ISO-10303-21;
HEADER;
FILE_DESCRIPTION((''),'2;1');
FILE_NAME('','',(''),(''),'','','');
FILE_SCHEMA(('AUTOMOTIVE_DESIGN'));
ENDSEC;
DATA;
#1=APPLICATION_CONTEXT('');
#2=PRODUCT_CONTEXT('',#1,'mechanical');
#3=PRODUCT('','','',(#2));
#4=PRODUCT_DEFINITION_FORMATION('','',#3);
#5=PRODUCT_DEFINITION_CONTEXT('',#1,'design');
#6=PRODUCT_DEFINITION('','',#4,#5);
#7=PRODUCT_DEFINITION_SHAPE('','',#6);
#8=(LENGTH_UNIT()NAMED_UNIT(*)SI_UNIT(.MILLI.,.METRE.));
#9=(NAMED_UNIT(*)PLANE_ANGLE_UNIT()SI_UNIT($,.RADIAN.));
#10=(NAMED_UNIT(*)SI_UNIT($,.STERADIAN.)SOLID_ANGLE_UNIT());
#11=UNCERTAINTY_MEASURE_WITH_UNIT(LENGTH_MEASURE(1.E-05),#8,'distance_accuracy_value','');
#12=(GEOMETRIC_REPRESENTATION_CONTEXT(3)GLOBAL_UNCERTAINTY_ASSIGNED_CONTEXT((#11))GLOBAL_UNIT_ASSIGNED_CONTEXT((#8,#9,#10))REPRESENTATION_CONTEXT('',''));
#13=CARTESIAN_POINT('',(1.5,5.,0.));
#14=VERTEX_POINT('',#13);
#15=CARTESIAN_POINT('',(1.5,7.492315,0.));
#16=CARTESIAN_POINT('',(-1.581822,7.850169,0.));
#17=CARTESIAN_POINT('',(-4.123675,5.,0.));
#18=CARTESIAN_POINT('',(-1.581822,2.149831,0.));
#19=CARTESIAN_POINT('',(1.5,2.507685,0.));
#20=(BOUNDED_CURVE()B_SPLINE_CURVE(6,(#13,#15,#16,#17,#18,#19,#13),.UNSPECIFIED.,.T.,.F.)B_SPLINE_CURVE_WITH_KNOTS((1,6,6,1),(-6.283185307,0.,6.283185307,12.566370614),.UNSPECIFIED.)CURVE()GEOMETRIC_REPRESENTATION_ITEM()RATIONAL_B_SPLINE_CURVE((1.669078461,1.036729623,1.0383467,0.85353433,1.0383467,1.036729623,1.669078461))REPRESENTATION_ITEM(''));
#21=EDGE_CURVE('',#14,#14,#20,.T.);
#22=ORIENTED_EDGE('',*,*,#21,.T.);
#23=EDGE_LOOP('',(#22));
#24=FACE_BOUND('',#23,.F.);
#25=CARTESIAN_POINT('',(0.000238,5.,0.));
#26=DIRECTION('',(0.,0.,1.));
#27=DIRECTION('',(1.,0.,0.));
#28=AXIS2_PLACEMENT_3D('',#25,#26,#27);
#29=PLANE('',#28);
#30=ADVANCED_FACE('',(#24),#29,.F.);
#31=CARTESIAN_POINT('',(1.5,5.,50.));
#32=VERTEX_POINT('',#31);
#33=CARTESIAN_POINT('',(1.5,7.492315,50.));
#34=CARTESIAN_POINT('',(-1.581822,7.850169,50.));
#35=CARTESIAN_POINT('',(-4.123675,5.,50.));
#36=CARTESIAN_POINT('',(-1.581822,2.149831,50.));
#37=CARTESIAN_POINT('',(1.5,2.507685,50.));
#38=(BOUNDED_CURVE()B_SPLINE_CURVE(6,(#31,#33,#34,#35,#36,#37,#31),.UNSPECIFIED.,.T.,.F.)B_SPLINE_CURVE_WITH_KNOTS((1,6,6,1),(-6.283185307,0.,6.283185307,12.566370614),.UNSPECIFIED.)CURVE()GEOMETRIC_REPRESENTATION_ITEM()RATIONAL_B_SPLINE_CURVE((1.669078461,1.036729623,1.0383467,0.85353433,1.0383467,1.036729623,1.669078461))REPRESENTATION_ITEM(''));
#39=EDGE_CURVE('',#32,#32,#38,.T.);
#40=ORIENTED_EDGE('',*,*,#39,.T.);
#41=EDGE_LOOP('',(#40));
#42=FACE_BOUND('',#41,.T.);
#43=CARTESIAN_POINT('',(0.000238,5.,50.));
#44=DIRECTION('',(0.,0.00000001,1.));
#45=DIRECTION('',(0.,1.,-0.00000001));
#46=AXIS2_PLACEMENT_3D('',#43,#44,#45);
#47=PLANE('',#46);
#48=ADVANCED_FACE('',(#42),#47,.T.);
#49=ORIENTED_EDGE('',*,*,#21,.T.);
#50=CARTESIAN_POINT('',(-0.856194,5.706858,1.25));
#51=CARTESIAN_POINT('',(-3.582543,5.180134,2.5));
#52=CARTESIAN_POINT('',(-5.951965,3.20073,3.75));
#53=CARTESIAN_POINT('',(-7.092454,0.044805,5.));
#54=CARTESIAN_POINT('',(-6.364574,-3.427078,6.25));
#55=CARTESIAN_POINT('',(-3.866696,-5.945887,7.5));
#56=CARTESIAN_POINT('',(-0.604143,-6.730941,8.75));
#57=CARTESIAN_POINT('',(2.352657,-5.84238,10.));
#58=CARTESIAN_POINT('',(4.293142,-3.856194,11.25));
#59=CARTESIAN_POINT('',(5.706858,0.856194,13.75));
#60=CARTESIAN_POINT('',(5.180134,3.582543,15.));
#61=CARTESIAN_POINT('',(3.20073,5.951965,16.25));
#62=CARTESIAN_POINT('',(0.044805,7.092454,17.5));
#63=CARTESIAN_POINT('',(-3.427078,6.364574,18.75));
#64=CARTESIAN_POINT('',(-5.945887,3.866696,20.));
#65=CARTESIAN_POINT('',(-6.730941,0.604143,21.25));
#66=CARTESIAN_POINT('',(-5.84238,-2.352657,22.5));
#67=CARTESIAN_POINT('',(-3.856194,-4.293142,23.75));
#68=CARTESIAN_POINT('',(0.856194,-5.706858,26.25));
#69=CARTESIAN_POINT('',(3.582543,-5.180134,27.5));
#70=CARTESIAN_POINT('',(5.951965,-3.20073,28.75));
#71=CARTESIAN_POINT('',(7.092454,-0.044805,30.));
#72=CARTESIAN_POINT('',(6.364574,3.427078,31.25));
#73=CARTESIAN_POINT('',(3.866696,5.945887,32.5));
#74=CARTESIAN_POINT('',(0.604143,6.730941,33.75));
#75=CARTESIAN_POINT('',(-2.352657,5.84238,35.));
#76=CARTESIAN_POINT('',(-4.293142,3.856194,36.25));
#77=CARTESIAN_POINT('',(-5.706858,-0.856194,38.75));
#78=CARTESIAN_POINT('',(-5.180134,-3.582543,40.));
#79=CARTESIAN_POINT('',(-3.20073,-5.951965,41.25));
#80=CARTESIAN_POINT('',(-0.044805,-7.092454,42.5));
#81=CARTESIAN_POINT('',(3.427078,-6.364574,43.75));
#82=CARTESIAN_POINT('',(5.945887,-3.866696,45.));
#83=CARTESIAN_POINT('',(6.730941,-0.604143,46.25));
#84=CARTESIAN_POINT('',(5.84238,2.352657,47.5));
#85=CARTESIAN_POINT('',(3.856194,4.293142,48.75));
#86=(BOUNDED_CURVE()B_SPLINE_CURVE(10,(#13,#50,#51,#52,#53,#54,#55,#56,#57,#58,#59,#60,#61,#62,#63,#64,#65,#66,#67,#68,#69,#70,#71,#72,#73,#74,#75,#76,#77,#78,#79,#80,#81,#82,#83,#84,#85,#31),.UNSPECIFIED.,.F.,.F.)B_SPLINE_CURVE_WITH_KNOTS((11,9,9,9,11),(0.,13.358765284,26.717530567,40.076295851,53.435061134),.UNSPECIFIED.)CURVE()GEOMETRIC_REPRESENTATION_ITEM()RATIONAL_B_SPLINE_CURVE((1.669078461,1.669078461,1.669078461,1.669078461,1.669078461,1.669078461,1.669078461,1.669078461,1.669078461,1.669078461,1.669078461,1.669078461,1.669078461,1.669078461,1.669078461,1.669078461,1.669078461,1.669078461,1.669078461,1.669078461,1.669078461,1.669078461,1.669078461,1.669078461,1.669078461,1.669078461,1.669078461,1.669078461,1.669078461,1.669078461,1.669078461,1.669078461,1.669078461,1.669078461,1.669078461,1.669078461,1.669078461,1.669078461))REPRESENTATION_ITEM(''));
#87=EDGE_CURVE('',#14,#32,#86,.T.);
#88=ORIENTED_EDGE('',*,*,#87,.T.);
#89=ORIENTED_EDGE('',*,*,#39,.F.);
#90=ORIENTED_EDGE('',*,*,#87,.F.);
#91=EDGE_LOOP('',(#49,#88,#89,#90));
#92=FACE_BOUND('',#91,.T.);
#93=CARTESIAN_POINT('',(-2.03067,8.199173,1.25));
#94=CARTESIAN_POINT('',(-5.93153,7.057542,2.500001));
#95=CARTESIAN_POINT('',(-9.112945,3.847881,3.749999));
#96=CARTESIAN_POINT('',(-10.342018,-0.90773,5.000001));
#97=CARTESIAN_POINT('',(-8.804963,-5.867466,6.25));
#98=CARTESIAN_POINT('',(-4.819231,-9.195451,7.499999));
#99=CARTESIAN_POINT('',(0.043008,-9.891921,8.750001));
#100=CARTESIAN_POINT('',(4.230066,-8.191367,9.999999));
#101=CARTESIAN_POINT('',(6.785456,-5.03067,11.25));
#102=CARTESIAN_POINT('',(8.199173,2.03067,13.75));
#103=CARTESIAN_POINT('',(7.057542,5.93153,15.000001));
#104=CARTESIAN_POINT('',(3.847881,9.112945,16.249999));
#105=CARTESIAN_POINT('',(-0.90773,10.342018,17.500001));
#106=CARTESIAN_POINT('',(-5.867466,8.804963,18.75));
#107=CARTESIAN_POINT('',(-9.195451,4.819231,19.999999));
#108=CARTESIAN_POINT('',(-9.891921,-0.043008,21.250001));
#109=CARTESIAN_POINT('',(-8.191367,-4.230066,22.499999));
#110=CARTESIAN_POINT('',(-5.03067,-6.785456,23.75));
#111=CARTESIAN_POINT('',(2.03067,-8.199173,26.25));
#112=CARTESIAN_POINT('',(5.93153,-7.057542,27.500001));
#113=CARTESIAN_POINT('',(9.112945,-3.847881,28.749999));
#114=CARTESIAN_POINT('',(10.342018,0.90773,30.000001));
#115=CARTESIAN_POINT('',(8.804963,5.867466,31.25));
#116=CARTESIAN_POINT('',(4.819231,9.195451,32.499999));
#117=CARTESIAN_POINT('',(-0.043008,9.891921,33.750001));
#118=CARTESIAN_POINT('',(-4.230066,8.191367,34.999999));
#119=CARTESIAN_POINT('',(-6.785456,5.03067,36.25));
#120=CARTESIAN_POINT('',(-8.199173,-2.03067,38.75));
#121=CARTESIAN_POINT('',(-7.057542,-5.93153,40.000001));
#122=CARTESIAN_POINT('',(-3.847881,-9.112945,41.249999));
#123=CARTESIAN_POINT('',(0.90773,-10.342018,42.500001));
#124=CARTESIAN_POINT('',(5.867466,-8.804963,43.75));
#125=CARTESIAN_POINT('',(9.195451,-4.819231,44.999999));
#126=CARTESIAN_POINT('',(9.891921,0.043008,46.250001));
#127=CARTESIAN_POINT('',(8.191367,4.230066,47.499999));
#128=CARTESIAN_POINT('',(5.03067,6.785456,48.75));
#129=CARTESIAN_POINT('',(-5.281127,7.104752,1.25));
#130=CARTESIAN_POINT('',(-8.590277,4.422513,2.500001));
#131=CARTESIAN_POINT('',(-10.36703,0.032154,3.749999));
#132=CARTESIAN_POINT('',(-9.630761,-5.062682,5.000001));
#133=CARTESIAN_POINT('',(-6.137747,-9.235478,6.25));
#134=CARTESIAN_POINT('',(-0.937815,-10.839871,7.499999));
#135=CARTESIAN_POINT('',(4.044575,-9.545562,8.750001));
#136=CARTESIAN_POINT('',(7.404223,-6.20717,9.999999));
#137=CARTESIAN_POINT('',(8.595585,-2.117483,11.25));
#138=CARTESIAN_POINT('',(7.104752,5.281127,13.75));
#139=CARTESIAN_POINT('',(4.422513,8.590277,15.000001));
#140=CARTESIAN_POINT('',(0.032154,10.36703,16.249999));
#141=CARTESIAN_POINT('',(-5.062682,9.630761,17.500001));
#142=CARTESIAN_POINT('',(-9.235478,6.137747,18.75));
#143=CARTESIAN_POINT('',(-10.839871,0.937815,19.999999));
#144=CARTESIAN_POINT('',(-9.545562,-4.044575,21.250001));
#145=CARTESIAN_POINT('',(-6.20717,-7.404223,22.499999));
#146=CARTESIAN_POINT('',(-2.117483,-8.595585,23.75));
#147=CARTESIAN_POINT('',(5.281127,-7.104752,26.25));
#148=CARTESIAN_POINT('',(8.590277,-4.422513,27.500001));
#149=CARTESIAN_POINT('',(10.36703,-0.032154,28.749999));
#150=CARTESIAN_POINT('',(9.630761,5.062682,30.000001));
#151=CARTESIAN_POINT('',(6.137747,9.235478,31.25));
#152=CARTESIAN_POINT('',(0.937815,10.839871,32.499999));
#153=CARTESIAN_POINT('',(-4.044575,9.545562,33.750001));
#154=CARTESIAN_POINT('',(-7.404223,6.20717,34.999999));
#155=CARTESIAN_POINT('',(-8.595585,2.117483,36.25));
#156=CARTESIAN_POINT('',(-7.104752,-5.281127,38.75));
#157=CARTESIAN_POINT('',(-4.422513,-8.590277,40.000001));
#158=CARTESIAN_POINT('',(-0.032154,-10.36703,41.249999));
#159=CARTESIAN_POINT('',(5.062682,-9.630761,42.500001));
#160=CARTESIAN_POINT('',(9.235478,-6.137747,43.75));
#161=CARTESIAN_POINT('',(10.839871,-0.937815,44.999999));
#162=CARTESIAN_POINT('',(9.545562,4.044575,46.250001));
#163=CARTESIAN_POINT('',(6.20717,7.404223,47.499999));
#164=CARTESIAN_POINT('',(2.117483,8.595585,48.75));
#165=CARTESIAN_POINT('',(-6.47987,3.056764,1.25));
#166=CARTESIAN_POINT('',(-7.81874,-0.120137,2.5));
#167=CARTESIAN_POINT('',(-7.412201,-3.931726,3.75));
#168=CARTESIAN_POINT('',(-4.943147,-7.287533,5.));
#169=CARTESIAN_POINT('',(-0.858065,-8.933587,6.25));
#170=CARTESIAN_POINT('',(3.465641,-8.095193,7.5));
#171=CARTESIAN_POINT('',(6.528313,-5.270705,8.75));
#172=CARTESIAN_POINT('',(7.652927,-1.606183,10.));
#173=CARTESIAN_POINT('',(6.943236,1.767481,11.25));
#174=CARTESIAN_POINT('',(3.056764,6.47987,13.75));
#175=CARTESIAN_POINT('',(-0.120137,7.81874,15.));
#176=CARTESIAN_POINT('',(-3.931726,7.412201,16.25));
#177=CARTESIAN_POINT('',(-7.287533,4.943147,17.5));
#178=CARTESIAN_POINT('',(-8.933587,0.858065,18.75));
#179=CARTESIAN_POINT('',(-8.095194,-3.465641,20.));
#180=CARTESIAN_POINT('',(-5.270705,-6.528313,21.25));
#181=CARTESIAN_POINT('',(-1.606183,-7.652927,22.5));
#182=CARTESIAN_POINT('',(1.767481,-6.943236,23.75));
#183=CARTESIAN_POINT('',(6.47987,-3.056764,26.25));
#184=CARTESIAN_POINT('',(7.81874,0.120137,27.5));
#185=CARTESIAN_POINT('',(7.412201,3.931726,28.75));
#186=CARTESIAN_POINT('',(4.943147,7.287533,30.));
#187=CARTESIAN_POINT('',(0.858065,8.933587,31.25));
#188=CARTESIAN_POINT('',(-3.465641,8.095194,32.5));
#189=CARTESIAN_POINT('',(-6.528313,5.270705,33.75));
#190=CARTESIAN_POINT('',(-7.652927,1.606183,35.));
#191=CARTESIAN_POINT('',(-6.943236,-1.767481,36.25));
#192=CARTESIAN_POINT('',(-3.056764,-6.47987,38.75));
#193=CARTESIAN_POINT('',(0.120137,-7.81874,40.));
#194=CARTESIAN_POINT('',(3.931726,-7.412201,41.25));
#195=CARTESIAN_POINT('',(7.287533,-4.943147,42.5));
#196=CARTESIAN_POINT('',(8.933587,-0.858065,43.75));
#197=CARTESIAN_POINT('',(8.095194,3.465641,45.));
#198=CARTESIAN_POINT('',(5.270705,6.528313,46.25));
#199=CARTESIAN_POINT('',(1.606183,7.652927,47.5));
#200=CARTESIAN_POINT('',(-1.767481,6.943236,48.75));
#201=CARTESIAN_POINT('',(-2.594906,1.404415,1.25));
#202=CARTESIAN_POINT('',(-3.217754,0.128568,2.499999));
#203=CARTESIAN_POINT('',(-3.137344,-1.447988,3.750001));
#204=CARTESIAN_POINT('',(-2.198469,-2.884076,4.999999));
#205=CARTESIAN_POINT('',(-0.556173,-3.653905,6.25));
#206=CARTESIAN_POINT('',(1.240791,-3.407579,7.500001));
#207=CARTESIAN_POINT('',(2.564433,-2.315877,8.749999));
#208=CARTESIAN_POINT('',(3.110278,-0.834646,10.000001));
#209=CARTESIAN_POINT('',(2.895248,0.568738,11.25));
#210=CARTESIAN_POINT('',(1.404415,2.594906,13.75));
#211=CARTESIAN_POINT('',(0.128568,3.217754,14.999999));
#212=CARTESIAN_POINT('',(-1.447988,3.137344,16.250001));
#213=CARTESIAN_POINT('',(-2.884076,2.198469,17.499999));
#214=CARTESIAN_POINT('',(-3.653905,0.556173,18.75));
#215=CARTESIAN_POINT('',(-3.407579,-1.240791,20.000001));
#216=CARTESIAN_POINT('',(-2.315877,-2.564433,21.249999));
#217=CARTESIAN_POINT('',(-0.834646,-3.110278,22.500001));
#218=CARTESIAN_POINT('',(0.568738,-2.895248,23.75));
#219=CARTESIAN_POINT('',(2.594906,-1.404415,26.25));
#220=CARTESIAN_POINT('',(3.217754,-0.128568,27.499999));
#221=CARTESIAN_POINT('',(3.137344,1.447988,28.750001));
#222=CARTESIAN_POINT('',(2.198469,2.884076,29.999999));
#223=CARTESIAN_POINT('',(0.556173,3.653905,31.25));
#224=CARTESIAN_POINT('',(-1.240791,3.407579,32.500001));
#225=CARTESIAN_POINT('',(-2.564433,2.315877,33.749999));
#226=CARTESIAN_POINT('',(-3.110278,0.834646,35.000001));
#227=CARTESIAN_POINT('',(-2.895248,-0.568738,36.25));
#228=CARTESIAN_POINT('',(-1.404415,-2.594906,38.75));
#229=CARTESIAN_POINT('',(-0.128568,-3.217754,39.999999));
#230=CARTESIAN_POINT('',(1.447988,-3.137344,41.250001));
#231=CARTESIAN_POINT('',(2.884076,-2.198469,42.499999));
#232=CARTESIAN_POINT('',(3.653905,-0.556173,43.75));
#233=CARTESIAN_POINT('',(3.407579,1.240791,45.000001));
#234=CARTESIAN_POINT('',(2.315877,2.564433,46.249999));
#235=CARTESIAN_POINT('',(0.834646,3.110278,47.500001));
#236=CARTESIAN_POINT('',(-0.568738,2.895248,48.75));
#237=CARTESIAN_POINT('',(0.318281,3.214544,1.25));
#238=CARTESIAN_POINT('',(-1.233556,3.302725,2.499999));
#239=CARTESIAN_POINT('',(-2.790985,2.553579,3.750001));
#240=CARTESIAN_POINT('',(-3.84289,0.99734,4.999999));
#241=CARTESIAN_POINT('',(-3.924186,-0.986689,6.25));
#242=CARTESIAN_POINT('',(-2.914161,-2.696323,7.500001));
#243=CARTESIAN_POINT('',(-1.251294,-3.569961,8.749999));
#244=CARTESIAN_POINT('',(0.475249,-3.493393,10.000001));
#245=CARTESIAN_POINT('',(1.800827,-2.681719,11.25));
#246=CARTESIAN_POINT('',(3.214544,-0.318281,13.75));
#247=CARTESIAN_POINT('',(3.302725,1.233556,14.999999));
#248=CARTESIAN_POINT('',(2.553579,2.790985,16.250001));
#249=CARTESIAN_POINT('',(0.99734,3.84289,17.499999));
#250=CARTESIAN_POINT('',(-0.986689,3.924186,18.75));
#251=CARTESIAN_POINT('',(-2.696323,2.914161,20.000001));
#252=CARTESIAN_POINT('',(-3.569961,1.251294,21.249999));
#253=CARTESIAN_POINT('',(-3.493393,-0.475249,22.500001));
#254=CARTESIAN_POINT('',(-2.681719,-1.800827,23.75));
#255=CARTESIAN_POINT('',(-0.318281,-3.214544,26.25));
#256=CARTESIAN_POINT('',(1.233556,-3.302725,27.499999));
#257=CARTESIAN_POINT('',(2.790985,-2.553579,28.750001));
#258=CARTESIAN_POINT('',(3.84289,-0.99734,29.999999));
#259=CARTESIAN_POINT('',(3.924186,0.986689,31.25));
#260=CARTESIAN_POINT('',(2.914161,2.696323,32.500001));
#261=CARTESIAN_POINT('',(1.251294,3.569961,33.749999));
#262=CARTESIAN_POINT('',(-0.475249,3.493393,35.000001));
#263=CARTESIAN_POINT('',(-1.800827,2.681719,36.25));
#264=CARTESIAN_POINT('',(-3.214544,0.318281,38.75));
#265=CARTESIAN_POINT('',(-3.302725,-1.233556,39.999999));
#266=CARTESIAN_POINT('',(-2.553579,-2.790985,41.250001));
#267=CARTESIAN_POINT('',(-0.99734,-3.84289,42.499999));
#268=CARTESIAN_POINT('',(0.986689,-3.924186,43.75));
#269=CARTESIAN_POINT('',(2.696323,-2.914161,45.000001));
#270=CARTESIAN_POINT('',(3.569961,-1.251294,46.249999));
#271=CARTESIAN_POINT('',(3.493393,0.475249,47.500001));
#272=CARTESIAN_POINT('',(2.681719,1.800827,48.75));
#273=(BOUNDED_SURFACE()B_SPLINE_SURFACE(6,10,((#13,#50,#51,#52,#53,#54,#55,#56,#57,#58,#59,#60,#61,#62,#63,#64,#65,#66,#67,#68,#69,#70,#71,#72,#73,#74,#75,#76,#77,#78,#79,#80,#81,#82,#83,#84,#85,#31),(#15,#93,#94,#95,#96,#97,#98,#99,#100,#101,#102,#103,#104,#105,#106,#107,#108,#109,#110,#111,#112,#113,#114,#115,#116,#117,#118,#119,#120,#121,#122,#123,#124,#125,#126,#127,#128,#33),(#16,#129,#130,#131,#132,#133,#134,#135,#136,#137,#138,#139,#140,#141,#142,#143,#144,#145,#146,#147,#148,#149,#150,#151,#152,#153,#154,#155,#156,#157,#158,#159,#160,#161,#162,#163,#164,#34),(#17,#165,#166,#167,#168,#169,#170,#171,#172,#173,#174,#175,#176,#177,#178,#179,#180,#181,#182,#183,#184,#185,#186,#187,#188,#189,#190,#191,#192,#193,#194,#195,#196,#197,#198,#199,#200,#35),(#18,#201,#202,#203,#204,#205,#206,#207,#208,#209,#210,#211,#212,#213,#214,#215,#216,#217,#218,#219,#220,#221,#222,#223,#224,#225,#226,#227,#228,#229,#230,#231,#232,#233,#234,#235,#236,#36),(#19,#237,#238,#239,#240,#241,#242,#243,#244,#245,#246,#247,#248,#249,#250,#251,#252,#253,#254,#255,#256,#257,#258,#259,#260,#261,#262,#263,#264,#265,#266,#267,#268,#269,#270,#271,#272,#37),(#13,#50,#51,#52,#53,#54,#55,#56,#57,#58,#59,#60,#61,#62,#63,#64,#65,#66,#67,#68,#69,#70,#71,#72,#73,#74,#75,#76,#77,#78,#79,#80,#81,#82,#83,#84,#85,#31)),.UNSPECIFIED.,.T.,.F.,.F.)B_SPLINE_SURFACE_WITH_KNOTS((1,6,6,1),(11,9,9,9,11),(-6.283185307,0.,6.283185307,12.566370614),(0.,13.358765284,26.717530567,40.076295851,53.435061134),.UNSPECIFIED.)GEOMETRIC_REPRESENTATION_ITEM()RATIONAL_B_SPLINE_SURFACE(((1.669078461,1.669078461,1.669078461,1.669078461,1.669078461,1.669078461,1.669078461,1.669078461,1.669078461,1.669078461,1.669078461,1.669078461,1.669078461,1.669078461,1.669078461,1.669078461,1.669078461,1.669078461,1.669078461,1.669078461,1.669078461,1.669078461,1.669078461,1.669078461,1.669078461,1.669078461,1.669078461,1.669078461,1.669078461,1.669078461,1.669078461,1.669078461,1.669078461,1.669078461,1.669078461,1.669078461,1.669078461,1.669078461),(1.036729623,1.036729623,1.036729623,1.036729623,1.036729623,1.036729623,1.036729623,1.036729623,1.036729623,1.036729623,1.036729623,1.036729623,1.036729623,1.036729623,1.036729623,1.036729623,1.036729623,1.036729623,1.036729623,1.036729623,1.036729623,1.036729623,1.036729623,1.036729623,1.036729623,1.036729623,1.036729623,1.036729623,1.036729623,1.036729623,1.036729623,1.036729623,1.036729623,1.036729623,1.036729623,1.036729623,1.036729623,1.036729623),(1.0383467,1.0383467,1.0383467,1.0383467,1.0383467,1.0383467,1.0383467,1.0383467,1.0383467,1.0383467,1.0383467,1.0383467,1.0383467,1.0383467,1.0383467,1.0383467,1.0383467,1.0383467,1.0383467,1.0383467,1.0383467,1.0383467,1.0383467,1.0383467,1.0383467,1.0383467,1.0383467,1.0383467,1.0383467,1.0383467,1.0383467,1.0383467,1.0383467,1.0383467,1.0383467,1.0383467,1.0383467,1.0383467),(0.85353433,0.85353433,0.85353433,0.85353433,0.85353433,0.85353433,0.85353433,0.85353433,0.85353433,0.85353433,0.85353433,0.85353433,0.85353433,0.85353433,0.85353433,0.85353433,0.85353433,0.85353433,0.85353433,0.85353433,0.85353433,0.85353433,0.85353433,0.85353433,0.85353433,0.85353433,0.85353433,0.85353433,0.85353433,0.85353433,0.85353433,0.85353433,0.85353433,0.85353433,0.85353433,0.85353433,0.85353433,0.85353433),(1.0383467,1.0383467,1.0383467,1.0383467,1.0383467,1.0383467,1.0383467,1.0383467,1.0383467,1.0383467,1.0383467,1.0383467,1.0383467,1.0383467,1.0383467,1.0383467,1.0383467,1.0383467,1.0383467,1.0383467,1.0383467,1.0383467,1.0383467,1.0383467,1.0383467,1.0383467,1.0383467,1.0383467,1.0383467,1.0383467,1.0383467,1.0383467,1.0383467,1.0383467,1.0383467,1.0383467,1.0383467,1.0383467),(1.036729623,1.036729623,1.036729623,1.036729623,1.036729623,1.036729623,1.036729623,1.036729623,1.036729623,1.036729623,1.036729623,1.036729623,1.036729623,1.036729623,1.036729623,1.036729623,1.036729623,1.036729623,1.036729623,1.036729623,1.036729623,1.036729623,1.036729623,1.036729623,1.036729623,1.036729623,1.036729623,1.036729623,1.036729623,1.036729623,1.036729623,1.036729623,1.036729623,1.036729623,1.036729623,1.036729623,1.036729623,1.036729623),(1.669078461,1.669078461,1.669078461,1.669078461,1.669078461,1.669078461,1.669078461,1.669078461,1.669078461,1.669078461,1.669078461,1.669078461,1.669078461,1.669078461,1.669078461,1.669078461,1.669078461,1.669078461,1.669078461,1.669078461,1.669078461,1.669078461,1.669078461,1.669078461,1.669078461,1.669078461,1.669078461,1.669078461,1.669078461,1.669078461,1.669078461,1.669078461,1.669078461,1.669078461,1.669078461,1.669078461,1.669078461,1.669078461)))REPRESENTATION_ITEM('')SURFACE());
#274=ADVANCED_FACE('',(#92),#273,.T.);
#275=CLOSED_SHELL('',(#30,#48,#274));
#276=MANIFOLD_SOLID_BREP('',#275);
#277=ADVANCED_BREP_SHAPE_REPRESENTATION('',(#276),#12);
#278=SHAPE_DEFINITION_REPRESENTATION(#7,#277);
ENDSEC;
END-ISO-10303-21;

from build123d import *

# Parameters (mm, degrees)
SPRING_COIL_PITCH       = 16.666666667
SPRING_COIL_HEIGHT      = 50
SPRING_COIL_RADIUS      = 5
SPRING_COIL_START_ANGLE = 90
WIRE_PROFILE_R          = 1.5


with BuildPart() as part:
    # Spring Coil: sweep along a helix
    with BuildLine() as spring_coil_path:
        add(Helix(SPRING_COIL_PITCH, SPRING_COIL_HEIGHT, SPRING_COIL_RADIUS, center=(0, 0, 0), direction=(0, 0, 1), mode=Mode.PRIVATE).rotate(Axis((0, 0, 0), (0, 0, 1)), SPRING_COIL_START_ANGLE))
    # Wire Profile → Spring Coil (sweep)
    with BuildSketch(Plane.XY):
        with Locations((0, 5)):
            Circle(WIRE_PROFILE_R)
    sweep(path=spring_coil_path.line, is_frenet=True)


solid = part.part
